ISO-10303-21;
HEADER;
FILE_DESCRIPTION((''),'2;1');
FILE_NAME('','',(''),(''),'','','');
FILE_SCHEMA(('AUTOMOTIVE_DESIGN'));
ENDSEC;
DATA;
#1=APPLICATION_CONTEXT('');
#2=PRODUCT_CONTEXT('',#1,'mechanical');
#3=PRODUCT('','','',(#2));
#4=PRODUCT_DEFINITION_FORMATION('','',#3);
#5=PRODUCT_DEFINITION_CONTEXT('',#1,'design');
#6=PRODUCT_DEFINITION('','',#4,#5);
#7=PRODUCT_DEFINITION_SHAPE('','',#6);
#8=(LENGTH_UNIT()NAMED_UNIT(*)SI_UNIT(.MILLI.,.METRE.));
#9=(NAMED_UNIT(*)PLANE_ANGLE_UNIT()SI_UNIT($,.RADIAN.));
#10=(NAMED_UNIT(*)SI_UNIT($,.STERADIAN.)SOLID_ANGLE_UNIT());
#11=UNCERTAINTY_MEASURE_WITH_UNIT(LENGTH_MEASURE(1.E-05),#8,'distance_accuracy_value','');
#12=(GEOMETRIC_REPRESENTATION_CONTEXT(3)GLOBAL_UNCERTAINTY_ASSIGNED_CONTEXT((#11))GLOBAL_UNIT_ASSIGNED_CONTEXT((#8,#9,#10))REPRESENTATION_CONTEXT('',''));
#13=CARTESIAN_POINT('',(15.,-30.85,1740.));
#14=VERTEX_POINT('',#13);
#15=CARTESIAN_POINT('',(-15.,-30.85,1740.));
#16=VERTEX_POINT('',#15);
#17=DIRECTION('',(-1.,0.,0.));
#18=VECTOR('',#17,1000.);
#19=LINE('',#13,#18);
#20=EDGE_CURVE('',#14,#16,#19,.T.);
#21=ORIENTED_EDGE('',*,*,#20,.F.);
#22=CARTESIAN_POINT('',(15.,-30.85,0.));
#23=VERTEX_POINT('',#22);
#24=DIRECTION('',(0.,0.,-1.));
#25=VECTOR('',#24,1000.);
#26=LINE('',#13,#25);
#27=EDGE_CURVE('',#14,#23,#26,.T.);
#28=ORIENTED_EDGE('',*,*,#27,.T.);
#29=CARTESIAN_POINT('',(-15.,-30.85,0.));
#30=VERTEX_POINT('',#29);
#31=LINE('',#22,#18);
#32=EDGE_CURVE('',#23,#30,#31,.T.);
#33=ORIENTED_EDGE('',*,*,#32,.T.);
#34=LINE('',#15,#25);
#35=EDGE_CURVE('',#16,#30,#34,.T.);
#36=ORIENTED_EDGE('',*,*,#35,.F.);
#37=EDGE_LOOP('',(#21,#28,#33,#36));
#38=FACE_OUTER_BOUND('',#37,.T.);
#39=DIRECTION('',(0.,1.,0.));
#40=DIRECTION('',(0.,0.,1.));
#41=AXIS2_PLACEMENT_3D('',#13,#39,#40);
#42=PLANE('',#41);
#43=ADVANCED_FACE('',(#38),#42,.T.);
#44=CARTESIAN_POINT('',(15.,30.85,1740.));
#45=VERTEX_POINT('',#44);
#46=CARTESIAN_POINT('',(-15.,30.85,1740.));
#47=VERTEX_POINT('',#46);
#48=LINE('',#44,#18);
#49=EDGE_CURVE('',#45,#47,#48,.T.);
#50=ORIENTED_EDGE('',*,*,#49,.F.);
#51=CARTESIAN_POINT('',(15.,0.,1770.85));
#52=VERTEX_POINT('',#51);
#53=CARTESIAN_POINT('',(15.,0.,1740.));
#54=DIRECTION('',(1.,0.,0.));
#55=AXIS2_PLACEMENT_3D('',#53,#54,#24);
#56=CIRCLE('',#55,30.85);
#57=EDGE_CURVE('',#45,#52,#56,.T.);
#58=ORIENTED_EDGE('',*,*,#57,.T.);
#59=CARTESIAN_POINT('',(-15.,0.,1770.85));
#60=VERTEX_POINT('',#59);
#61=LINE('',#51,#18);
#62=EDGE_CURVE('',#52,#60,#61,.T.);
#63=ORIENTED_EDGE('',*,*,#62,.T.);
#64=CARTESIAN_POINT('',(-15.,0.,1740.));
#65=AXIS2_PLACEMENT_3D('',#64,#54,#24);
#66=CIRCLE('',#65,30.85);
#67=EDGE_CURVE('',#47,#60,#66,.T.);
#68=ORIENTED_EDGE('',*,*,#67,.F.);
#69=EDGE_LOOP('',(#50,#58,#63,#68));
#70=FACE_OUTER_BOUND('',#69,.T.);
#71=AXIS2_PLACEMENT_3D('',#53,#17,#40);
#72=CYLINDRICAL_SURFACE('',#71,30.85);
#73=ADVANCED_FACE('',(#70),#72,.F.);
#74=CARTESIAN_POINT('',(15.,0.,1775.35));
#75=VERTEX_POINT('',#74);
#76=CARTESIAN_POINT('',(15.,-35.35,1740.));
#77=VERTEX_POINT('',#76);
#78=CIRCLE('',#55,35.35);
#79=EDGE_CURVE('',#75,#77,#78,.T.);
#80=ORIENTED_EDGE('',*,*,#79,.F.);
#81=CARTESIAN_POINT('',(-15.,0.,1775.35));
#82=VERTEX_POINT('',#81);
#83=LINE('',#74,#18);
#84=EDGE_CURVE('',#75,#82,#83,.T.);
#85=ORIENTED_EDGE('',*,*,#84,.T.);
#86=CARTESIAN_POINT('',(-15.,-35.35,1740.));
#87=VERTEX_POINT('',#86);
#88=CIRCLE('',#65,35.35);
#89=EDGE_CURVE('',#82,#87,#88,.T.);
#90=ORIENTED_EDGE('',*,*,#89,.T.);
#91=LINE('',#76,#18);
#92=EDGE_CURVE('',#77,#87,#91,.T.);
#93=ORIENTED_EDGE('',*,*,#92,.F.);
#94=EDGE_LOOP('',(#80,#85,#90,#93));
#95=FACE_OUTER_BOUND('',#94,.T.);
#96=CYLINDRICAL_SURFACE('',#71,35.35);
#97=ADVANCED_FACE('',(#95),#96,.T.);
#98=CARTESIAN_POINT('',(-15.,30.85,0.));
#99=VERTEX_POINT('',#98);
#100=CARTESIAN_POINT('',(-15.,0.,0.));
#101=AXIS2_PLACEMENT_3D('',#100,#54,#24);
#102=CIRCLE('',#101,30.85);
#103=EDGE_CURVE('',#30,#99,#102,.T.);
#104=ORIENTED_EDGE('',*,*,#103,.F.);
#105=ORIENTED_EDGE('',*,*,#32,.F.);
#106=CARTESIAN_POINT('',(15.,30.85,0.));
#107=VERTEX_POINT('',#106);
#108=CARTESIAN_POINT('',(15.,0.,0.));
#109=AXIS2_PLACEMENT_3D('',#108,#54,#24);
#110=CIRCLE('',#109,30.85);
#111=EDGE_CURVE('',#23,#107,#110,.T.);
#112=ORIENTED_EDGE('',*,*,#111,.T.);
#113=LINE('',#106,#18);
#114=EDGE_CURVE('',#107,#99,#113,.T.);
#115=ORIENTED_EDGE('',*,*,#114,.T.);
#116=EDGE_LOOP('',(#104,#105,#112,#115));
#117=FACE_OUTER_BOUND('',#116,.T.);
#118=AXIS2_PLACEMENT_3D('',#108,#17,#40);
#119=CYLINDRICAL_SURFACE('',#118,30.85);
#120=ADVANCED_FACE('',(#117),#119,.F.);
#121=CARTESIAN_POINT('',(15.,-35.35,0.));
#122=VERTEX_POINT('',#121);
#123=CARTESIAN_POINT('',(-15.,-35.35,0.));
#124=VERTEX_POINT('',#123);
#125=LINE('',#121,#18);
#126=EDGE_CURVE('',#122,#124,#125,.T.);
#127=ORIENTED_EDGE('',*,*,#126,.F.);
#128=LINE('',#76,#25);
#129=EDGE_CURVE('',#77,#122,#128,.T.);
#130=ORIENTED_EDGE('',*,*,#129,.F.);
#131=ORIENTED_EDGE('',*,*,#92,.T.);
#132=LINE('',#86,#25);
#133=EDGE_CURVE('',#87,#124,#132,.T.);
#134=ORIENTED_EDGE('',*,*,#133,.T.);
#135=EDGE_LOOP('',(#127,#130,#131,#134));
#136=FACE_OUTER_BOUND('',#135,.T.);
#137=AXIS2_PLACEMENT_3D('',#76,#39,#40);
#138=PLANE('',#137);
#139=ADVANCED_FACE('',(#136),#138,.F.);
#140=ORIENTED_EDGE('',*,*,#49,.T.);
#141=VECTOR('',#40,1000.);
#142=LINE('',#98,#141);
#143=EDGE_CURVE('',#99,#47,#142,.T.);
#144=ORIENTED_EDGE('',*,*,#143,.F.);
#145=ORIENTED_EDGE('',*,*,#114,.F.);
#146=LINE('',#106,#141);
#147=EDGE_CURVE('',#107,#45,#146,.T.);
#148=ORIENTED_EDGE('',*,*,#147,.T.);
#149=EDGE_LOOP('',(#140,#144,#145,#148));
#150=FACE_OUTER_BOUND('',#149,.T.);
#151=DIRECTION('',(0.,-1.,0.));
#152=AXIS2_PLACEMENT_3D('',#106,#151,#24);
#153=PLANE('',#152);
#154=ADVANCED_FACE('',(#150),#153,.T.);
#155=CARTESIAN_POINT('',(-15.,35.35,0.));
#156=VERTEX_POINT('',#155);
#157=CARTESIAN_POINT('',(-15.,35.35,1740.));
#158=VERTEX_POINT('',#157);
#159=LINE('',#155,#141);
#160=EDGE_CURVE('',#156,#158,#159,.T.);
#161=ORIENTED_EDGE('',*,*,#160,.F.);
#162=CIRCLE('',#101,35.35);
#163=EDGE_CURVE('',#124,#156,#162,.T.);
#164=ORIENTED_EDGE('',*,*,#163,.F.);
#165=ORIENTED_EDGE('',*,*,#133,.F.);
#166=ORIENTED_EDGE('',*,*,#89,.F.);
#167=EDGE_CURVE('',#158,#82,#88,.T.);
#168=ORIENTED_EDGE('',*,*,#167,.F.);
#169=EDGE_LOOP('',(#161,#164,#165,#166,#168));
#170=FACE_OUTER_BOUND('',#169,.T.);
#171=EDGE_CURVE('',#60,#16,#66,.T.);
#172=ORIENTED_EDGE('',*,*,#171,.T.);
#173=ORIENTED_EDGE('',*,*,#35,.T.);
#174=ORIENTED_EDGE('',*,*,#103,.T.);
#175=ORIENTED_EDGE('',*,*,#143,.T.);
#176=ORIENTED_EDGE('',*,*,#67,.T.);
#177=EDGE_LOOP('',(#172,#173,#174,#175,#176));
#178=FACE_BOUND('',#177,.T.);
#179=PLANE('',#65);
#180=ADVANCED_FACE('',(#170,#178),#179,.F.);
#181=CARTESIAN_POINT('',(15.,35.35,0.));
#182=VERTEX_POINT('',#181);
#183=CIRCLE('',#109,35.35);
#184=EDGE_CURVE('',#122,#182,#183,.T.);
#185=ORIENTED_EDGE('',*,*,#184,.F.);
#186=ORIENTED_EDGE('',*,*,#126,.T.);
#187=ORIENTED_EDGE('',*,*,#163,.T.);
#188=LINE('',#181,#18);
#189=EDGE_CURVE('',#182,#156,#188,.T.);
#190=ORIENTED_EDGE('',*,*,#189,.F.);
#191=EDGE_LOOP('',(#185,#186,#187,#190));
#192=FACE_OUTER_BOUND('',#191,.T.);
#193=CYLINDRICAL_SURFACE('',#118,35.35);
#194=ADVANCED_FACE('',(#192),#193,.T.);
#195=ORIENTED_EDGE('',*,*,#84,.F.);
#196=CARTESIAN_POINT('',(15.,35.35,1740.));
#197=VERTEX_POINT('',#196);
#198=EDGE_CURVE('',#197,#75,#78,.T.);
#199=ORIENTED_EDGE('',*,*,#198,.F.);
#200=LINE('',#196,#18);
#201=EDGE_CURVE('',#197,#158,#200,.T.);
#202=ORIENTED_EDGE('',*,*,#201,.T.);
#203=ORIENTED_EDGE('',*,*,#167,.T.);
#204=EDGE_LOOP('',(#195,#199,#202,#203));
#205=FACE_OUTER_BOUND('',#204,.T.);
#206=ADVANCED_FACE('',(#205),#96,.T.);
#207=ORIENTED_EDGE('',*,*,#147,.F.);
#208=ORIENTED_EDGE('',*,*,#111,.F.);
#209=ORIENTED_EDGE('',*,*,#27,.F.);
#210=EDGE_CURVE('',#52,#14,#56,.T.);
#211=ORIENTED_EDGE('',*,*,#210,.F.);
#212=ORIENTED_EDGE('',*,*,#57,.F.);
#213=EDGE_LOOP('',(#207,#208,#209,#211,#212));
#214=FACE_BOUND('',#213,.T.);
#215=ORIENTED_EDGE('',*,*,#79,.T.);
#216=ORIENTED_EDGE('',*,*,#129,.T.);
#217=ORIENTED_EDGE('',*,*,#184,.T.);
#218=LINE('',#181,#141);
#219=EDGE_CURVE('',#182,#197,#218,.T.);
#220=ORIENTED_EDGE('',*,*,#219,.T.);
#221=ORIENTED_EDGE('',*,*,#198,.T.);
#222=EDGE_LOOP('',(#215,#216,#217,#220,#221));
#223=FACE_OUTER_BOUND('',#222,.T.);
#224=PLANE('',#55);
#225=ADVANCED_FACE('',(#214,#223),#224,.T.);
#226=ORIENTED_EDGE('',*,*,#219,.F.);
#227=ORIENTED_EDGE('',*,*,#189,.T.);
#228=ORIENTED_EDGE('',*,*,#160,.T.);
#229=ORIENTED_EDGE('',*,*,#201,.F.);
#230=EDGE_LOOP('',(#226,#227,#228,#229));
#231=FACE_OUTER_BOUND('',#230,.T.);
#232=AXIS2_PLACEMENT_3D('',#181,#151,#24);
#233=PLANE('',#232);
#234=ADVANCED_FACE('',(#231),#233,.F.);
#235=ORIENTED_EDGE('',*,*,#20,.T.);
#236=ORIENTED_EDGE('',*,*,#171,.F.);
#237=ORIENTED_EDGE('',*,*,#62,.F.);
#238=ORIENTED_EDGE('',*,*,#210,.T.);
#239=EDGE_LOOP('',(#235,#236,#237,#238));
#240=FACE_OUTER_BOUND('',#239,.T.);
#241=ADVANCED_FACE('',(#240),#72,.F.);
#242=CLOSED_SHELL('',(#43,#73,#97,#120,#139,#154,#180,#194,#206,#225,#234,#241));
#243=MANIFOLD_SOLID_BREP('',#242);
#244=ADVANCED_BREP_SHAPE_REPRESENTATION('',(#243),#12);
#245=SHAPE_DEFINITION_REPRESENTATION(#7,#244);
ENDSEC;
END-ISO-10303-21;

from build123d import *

# Parameters (mm, degrees)
EXTRUDE_1_DEPTH = 15


with BuildPart() as part:
    # 草图2 → 拉伸-薄壁1 (new, symmetric)
    with BuildSketch(Plane(origin=(0, 0, 0), x_dir=(0, 0, -1), z_dir=(1, 0, 0))):
        with BuildLine():
            Line((-1740, -35.35), (0, -35.35))
            ThreePointArc((0, -35.35), (35.35, 0), (0, 35.35))
            Line((0, 35.35), (-1740, 35.35))
            ThreePointArc((-1740, 35.35), (-1775.35, 0), (-1740, -35.35))
        make_face()
        with BuildLine():
            Line((-1740, -30.85), (0, -30.85))
            ThreePointArc((0, -30.85), (30.85, 0), (0, 30.85))
            Line((0, 30.85), (-1740, 30.85))
            ThreePointArc((-1740, 30.85), (-1770.85, 0), (-1740, -30.85))
        make_face(mode=Mode.SUBTRACT)
    extrude(amount=EXTRUDE_1_DEPTH, both=True)


solid = part.part
